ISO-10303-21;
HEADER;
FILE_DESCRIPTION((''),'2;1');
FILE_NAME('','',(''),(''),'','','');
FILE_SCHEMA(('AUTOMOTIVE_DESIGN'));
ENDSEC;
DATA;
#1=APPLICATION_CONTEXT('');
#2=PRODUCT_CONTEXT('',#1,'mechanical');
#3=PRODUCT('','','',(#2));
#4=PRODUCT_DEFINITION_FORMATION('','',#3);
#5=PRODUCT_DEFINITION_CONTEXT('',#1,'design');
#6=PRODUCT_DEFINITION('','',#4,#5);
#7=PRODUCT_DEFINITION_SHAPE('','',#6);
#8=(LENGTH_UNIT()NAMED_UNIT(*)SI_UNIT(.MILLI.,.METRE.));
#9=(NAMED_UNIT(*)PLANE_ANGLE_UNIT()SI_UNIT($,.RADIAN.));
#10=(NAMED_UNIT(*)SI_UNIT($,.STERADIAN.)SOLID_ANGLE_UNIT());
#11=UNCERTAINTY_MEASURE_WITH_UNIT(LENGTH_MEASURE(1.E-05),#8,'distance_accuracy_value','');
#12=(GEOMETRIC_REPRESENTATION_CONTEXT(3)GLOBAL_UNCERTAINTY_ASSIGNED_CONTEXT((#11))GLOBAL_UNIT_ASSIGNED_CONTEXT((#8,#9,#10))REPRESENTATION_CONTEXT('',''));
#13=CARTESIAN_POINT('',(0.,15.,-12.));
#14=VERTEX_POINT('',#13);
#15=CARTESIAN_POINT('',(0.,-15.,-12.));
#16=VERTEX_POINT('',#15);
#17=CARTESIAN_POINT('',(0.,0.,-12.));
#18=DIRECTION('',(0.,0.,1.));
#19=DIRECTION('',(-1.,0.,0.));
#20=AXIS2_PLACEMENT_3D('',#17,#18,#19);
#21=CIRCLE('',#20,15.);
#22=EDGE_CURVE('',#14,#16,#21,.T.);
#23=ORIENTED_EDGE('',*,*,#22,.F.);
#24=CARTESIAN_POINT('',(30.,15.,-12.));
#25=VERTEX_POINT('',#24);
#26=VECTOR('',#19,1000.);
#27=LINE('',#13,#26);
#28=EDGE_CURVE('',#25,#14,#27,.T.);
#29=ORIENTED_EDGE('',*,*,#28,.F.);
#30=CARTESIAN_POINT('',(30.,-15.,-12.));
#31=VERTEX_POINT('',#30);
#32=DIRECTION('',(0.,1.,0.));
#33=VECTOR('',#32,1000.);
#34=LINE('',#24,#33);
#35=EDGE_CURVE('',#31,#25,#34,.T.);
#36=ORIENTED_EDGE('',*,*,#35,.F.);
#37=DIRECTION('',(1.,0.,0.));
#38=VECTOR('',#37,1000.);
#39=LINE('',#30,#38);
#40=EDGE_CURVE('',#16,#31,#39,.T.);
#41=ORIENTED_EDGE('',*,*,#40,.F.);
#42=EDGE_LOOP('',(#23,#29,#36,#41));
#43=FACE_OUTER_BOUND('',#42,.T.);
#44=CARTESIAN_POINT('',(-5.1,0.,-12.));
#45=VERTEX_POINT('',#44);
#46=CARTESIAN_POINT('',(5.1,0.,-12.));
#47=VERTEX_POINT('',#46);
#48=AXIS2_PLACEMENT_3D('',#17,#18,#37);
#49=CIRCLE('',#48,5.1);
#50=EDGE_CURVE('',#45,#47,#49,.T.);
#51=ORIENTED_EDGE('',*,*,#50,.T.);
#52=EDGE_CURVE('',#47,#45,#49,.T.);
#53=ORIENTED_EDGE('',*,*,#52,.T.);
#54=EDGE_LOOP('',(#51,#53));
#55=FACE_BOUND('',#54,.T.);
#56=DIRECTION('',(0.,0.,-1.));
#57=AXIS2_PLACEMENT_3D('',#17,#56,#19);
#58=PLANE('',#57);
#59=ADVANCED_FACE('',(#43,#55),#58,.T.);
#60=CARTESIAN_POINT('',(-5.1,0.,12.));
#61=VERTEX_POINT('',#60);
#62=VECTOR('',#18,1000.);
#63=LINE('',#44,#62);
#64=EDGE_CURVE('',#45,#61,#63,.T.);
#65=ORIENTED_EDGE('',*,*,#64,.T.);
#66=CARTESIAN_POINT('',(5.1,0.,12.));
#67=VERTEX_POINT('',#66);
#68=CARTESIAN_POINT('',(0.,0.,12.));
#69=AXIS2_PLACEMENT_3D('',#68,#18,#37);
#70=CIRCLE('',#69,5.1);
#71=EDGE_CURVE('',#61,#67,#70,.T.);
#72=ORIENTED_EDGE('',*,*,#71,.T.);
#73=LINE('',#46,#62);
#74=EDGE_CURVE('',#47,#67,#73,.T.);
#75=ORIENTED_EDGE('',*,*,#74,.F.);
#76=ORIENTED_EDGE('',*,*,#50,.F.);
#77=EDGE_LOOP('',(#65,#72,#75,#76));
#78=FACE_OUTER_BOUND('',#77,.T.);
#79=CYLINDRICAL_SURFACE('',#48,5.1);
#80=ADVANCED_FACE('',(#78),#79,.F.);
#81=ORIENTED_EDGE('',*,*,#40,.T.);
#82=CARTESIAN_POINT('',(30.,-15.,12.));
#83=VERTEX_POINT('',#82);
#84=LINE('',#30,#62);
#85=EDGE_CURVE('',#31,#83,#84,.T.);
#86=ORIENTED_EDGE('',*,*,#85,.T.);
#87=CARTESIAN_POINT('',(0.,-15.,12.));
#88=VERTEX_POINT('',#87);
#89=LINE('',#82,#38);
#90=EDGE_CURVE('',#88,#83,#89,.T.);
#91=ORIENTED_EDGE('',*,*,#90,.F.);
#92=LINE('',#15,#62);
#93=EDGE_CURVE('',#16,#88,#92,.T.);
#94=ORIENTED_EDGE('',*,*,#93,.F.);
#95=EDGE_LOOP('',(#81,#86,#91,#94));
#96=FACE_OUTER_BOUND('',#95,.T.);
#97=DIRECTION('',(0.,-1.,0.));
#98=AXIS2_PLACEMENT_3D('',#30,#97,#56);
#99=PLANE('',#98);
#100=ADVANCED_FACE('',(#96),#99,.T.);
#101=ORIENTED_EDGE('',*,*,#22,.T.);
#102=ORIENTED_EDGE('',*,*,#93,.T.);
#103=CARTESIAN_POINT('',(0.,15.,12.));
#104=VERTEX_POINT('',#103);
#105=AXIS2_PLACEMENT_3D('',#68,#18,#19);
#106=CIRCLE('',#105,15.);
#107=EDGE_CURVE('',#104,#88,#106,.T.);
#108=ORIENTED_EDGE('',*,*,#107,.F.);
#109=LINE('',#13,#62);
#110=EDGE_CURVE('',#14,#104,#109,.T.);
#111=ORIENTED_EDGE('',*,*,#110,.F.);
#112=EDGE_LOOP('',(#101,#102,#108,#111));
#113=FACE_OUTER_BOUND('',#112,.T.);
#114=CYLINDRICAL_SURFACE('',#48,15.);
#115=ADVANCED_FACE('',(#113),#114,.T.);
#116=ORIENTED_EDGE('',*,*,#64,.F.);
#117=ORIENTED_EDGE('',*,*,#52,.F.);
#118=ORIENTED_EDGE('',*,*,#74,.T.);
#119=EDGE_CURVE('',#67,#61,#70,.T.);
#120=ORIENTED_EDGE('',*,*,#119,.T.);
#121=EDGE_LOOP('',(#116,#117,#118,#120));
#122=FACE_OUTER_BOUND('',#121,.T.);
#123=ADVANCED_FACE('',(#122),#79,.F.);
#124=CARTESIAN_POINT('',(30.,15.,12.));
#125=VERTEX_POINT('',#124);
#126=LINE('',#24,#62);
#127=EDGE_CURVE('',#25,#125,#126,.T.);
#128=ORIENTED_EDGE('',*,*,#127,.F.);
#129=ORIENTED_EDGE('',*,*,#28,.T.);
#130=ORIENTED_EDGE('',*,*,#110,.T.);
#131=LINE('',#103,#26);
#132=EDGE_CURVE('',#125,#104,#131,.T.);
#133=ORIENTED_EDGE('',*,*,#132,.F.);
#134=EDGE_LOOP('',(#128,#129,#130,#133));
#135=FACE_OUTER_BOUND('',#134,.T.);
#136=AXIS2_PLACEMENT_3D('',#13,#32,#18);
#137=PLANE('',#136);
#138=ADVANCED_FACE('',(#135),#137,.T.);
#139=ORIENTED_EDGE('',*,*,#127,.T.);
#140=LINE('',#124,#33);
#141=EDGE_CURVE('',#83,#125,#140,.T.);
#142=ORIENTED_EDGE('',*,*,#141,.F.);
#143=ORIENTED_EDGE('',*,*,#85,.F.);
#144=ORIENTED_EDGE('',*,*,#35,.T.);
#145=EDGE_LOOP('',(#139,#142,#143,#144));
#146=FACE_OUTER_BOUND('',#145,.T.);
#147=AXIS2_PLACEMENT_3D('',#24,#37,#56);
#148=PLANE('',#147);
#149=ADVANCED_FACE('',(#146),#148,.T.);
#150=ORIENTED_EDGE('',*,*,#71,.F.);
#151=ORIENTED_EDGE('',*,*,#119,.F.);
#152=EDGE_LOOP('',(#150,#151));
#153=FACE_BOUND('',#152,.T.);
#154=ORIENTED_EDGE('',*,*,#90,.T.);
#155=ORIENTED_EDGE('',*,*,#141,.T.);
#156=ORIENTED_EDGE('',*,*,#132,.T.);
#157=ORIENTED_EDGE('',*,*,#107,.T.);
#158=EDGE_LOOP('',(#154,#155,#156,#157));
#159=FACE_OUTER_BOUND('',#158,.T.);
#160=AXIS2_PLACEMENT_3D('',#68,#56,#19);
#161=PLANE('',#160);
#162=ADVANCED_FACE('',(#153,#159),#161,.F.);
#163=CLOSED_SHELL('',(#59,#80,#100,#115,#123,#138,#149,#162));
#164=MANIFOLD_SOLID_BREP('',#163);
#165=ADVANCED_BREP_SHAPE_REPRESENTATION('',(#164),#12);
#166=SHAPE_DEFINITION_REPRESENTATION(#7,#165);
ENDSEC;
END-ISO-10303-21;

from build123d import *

# Parameters (mm, degrees)
SKETCH_1_R      = 5.1
EXTRUDE_1_DEPTH = 12


with BuildPart() as part:
    # 草图1 → 凸台-拉伸1 (new, symmetric)
    with BuildSketch(Plane.XY):
        with BuildLine():
            Line((0, 15), (30, 15))
            Line((30, 15), (30, -15))
            Line((30, -15), (0, -15))
            ThreePointArc((0, -15), (-15, 0), (0, 15))
        make_face()
        Circle(SKETCH_1_R, mode=Mode.SUBTRACT)
    extrude(amount=EXTRUDE_1_DEPTH, both=True)


solid = part.part
